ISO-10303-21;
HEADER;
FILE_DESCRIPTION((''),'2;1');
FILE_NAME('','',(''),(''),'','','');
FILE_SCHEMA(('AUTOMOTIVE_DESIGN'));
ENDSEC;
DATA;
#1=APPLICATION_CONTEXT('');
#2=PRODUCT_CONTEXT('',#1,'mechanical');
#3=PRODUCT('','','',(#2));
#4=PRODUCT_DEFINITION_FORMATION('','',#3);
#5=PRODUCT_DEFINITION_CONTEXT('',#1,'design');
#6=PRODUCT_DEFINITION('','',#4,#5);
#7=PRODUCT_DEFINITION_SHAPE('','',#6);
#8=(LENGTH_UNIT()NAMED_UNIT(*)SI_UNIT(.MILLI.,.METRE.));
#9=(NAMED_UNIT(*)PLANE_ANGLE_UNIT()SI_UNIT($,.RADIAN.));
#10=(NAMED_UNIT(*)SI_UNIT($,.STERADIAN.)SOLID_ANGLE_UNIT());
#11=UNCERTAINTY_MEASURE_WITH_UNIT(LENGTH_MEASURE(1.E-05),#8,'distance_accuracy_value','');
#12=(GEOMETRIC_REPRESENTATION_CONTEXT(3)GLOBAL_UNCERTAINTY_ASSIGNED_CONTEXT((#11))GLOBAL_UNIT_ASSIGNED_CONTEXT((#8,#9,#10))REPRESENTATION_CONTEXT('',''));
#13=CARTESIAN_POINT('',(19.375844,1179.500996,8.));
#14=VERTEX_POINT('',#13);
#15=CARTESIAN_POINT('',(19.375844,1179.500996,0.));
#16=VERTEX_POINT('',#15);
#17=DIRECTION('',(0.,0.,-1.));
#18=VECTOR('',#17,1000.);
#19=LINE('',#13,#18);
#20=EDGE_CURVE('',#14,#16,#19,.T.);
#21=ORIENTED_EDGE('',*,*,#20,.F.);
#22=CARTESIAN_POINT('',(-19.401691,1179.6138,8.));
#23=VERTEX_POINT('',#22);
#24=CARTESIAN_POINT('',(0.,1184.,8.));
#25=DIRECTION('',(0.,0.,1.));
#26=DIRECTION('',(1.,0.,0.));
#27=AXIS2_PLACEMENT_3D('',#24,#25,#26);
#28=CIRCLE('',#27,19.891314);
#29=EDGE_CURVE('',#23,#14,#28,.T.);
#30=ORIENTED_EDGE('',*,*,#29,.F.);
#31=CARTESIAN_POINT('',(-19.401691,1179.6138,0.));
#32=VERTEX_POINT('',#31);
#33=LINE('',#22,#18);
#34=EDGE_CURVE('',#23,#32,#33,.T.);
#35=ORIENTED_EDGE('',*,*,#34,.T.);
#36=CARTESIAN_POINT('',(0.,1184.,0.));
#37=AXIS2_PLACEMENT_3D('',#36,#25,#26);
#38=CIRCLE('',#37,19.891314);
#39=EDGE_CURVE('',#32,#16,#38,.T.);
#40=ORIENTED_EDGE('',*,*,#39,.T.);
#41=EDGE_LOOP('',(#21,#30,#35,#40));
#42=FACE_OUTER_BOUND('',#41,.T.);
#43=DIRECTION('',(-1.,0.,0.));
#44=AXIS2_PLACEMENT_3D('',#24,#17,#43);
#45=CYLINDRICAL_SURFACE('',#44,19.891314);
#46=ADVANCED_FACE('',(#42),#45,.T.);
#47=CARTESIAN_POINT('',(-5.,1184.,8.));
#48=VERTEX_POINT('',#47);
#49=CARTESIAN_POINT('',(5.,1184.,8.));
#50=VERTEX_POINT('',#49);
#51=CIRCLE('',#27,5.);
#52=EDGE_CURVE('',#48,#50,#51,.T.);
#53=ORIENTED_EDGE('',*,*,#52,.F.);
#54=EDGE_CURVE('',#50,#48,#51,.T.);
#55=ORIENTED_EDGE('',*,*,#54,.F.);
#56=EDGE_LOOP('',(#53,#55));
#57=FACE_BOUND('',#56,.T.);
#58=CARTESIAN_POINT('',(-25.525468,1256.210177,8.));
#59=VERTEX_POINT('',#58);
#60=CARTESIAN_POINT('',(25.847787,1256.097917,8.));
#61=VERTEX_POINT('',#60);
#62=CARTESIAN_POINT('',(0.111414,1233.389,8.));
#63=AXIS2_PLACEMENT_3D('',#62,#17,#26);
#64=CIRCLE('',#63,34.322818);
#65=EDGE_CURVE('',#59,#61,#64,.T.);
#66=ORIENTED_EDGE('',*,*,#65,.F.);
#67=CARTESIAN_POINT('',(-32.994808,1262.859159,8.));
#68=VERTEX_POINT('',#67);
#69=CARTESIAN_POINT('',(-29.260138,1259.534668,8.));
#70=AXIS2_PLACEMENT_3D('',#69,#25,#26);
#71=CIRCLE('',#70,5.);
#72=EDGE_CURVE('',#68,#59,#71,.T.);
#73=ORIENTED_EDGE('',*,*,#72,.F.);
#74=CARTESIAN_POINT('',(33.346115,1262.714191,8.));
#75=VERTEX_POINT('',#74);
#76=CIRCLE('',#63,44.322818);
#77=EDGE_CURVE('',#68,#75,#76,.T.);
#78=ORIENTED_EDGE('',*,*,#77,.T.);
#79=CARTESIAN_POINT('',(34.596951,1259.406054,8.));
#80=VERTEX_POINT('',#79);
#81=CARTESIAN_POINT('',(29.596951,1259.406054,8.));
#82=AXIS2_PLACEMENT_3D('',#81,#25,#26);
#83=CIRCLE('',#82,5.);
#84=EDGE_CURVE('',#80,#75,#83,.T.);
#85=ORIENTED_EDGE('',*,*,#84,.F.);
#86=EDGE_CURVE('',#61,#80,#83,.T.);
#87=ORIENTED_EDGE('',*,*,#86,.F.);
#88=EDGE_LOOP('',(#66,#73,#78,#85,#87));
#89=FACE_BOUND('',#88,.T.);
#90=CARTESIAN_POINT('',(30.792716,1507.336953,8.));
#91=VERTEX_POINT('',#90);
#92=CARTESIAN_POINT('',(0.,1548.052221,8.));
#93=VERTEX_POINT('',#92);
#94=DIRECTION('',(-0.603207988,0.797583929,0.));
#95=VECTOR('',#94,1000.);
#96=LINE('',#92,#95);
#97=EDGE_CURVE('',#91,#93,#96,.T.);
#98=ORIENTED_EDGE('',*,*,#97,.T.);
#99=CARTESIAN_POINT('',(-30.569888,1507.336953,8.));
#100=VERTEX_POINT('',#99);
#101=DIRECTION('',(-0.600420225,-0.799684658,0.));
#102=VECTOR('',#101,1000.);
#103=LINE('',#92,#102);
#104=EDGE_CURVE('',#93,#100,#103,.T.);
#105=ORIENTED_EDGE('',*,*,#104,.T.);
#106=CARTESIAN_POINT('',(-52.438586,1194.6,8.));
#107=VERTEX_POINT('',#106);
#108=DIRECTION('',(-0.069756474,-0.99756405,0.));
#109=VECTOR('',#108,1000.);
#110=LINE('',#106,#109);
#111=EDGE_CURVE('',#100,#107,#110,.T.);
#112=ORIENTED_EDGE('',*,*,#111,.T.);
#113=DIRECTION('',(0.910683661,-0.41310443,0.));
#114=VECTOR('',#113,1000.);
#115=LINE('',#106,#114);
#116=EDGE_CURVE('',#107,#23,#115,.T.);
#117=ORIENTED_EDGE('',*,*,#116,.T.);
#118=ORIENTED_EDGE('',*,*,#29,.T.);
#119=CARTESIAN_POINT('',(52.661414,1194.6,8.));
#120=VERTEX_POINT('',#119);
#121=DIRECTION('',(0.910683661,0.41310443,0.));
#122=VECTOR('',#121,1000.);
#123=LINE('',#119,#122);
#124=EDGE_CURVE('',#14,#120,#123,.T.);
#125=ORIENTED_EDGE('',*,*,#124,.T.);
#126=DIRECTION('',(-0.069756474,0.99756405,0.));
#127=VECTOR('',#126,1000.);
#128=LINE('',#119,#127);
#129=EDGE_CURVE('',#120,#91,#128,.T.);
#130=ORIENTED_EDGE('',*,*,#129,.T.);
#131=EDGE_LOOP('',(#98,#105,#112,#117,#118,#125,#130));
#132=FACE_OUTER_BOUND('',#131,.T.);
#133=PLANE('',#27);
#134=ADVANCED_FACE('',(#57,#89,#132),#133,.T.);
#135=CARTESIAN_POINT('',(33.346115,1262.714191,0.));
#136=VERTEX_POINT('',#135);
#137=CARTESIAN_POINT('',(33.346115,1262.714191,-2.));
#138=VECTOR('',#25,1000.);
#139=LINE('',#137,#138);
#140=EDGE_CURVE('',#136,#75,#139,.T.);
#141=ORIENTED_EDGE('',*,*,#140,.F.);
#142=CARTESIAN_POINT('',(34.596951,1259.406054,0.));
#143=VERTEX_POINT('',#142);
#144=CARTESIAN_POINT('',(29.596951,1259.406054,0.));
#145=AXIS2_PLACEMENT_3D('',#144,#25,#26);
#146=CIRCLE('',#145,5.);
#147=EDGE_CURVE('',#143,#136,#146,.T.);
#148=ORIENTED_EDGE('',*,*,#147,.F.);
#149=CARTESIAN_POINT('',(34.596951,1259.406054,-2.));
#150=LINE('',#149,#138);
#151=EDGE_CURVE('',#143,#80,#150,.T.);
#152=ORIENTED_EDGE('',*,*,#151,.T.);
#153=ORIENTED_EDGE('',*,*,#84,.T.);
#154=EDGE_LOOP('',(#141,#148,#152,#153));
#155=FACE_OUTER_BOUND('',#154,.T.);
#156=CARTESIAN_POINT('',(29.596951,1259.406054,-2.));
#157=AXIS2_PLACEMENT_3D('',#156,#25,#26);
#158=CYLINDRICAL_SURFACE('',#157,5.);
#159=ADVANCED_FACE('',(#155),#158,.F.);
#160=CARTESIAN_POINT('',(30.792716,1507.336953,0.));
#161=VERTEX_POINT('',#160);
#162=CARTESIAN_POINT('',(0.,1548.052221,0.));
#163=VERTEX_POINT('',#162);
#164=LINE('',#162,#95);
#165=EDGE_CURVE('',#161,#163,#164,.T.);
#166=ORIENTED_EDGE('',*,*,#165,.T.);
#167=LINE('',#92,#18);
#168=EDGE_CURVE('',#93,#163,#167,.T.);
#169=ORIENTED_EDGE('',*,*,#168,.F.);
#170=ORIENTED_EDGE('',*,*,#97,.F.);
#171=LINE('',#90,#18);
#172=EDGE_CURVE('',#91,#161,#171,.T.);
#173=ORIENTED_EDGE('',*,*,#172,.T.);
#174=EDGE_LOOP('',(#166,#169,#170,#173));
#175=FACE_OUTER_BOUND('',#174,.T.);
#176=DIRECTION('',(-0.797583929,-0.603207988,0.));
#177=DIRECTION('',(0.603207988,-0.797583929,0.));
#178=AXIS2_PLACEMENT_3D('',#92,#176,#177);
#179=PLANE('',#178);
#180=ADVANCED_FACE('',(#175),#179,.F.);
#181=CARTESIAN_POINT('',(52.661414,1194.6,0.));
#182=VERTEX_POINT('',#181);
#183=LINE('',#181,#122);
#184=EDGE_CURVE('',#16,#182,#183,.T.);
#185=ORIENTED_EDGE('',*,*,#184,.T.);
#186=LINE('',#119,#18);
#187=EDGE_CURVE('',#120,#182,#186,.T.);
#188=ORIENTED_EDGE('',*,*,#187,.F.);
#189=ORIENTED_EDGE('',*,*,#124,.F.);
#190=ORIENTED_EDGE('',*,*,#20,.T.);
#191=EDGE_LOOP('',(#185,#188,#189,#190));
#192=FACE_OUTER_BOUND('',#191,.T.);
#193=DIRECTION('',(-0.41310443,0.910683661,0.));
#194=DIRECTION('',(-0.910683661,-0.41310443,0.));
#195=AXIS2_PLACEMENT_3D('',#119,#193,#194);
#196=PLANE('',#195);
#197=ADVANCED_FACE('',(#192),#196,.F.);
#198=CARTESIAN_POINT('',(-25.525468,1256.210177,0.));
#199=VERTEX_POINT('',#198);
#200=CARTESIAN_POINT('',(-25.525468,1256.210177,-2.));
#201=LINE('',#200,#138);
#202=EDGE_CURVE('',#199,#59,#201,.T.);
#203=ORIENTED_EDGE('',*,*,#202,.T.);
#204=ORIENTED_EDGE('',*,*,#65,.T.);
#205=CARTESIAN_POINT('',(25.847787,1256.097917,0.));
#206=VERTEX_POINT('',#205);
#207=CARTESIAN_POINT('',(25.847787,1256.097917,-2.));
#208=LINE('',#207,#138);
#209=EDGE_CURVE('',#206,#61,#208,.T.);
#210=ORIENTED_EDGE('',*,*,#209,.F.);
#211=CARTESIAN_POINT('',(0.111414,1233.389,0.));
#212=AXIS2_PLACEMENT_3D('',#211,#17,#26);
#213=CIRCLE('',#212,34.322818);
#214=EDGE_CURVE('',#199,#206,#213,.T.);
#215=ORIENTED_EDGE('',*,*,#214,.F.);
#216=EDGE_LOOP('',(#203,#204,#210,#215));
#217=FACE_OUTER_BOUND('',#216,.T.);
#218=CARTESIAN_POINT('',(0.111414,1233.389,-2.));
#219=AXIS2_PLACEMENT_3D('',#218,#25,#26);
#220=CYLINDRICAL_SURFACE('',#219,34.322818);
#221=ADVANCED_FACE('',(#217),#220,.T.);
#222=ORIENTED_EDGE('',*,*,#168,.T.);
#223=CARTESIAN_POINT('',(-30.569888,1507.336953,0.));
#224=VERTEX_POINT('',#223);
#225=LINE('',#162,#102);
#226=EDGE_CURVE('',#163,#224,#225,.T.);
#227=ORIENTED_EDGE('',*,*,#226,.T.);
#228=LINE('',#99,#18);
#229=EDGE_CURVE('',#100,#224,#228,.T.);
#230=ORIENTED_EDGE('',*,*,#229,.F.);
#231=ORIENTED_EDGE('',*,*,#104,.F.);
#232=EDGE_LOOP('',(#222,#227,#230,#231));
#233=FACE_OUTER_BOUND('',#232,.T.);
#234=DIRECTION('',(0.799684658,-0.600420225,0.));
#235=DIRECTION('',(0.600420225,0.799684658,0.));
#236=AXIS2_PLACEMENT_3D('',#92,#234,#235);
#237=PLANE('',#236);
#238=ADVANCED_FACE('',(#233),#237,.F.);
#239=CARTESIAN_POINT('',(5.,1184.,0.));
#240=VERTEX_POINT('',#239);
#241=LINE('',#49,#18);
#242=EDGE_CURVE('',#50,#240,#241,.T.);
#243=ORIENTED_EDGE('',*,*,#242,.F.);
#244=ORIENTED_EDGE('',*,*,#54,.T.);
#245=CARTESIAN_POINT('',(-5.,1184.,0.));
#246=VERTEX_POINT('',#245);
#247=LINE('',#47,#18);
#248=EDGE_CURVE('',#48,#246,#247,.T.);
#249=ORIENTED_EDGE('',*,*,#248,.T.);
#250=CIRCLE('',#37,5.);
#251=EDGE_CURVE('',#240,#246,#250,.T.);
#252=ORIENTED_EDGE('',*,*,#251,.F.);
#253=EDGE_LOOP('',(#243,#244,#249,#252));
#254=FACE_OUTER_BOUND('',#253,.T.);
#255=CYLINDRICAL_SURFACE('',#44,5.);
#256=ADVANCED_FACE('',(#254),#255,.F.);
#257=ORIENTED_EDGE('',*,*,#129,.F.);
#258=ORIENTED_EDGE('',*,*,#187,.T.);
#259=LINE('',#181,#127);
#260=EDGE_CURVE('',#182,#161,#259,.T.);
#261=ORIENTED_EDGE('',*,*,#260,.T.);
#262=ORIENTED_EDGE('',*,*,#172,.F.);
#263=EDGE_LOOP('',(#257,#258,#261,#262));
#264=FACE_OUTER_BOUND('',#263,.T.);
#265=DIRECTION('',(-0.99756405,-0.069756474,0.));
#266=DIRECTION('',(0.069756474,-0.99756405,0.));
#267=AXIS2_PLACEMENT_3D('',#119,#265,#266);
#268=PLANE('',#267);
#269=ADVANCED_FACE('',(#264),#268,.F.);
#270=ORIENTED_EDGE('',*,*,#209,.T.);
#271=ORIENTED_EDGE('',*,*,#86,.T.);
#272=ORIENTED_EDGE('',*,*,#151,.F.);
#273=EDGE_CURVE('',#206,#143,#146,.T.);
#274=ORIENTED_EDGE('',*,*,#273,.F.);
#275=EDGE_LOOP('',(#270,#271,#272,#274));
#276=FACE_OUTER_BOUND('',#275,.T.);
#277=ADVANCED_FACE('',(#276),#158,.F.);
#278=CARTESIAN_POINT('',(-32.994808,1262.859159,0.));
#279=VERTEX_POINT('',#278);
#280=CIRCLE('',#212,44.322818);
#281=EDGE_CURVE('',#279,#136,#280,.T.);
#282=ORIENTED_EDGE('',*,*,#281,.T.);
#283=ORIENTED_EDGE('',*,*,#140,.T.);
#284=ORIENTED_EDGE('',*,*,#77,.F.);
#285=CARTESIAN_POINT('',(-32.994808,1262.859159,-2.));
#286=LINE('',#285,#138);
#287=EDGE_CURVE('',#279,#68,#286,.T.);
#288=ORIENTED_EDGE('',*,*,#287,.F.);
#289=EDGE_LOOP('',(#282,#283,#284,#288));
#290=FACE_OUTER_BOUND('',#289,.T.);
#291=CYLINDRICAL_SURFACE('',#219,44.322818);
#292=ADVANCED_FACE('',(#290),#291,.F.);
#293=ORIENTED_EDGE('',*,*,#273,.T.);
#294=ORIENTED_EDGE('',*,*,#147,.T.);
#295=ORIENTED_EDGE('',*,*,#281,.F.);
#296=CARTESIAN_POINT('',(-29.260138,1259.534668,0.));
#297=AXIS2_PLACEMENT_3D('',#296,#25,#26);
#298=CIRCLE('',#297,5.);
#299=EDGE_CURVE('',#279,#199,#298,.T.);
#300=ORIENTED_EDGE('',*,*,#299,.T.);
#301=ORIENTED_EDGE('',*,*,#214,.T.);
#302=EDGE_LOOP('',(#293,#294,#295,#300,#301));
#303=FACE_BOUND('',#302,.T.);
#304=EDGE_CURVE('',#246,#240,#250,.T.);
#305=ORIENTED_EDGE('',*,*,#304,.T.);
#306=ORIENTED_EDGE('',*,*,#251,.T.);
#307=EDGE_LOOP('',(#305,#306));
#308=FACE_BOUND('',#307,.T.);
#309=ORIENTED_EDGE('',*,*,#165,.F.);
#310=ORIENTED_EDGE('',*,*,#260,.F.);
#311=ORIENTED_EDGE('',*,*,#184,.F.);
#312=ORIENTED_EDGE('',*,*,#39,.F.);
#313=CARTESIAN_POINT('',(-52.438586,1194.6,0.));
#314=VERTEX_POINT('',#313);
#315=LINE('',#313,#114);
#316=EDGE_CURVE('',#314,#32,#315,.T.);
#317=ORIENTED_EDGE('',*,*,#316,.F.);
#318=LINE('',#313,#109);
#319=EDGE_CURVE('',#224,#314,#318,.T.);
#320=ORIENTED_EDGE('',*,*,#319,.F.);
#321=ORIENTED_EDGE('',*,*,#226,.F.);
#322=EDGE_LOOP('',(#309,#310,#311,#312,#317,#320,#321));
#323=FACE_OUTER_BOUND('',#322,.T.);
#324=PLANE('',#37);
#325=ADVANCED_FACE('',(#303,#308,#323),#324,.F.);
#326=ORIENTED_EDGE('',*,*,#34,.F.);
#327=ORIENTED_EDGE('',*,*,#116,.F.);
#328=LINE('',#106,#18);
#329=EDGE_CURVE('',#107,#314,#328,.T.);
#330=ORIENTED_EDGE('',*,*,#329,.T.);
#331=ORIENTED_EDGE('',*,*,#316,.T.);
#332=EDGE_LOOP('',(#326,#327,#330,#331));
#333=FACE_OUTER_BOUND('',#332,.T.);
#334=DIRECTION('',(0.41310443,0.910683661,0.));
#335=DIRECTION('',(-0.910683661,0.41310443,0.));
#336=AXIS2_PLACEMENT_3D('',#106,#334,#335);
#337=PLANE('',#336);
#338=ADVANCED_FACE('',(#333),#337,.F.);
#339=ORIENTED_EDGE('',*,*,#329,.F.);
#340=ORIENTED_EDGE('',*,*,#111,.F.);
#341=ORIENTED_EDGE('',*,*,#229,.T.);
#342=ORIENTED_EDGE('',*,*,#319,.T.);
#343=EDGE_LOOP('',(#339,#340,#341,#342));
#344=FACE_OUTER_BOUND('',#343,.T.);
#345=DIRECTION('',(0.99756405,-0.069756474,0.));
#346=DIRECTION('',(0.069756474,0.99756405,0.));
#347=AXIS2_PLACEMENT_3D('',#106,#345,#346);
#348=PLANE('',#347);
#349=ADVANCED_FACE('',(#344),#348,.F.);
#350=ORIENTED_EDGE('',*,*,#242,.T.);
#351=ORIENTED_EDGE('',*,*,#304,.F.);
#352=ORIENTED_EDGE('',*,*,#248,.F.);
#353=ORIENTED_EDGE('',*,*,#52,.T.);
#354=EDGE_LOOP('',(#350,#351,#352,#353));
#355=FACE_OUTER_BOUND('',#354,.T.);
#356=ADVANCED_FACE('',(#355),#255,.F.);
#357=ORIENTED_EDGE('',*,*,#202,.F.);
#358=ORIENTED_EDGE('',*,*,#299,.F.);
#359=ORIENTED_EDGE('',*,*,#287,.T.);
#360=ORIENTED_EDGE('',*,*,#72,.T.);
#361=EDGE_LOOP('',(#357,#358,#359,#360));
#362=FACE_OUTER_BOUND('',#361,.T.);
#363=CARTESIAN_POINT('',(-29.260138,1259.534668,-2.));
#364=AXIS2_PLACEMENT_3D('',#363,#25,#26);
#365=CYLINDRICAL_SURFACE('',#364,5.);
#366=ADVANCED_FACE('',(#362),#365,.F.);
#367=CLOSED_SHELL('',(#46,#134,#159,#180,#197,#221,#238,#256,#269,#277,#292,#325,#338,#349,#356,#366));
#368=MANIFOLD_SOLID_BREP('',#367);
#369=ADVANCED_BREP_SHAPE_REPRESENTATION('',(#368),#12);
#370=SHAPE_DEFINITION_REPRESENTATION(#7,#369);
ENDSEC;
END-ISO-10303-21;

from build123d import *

# Parameters (mm, degrees)
SKETCH2_R           = 5
BOSS_EXTRUDE1_DEPTH = 8
CUT_EXTRUDE1_DEPTH  = 10


with BuildPart() as part:
    # Sketch2 → Boss-Extrude1 (new body)
    with BuildSketch(Plane.XY):
        with BuildLine():
            Line((52.661413708, 1194.6), (30.792715617, 1507.336952872))
            Line((30.792715617, 1507.336952872), (0, 1548.052221237))
            Line((0, 1548.052221237), (-30.569888201, 1507.336952872))
            Line((-30.569888201, 1507.336952872), (-52.438586292, 1194.6))
            Line((-52.438586292, 1194.6), (-19.401690748, 1179.61379954))
            ThreePointArc((-19.401690748, 1179.61379954), (-0.057863528, 1164.108770521), (19.375843714, 1179.500995806))
            Line((19.375843714, 1179.500995806), (52.661413708, 1194.6))
        make_face()
        with Locations((0, 1184)):
            Circle(SKETCH2_R, mode=Mode.SUBTRACT)
    extrude(amount=BOSS_EXTRUDE1_DEPTH)

    # Sketch3 → Cut-Extrude1 (cut)
    with BuildSketch(Plane.XY.offset(8)):
        with BuildLine():
            ThreePointArc((33.346114696, 1262.714191316), (0.208267219, 1277.711712086), (-32.994808317, 1262.859158782))
            ThreePointArc((-32.994808317, 1262.859158782), (-32.584628739, 1255.799997875), (-25.525467832, 1256.210177452))
            ThreePointArc((-25.525467832, 1256.210177452), (0.186415379, 1267.711735961), (25.847787119, 1256.097917173))
            ThreePointArc((25.847787119, 1256.097917173), (32.905087979, 1255.656890456), (33.346114696, 1262.714191316))
        make_face()
    extrude(amount=-CUT_EXTRUDE1_DEPTH, mode=Mode.SUBTRACT)


solid = part.part
